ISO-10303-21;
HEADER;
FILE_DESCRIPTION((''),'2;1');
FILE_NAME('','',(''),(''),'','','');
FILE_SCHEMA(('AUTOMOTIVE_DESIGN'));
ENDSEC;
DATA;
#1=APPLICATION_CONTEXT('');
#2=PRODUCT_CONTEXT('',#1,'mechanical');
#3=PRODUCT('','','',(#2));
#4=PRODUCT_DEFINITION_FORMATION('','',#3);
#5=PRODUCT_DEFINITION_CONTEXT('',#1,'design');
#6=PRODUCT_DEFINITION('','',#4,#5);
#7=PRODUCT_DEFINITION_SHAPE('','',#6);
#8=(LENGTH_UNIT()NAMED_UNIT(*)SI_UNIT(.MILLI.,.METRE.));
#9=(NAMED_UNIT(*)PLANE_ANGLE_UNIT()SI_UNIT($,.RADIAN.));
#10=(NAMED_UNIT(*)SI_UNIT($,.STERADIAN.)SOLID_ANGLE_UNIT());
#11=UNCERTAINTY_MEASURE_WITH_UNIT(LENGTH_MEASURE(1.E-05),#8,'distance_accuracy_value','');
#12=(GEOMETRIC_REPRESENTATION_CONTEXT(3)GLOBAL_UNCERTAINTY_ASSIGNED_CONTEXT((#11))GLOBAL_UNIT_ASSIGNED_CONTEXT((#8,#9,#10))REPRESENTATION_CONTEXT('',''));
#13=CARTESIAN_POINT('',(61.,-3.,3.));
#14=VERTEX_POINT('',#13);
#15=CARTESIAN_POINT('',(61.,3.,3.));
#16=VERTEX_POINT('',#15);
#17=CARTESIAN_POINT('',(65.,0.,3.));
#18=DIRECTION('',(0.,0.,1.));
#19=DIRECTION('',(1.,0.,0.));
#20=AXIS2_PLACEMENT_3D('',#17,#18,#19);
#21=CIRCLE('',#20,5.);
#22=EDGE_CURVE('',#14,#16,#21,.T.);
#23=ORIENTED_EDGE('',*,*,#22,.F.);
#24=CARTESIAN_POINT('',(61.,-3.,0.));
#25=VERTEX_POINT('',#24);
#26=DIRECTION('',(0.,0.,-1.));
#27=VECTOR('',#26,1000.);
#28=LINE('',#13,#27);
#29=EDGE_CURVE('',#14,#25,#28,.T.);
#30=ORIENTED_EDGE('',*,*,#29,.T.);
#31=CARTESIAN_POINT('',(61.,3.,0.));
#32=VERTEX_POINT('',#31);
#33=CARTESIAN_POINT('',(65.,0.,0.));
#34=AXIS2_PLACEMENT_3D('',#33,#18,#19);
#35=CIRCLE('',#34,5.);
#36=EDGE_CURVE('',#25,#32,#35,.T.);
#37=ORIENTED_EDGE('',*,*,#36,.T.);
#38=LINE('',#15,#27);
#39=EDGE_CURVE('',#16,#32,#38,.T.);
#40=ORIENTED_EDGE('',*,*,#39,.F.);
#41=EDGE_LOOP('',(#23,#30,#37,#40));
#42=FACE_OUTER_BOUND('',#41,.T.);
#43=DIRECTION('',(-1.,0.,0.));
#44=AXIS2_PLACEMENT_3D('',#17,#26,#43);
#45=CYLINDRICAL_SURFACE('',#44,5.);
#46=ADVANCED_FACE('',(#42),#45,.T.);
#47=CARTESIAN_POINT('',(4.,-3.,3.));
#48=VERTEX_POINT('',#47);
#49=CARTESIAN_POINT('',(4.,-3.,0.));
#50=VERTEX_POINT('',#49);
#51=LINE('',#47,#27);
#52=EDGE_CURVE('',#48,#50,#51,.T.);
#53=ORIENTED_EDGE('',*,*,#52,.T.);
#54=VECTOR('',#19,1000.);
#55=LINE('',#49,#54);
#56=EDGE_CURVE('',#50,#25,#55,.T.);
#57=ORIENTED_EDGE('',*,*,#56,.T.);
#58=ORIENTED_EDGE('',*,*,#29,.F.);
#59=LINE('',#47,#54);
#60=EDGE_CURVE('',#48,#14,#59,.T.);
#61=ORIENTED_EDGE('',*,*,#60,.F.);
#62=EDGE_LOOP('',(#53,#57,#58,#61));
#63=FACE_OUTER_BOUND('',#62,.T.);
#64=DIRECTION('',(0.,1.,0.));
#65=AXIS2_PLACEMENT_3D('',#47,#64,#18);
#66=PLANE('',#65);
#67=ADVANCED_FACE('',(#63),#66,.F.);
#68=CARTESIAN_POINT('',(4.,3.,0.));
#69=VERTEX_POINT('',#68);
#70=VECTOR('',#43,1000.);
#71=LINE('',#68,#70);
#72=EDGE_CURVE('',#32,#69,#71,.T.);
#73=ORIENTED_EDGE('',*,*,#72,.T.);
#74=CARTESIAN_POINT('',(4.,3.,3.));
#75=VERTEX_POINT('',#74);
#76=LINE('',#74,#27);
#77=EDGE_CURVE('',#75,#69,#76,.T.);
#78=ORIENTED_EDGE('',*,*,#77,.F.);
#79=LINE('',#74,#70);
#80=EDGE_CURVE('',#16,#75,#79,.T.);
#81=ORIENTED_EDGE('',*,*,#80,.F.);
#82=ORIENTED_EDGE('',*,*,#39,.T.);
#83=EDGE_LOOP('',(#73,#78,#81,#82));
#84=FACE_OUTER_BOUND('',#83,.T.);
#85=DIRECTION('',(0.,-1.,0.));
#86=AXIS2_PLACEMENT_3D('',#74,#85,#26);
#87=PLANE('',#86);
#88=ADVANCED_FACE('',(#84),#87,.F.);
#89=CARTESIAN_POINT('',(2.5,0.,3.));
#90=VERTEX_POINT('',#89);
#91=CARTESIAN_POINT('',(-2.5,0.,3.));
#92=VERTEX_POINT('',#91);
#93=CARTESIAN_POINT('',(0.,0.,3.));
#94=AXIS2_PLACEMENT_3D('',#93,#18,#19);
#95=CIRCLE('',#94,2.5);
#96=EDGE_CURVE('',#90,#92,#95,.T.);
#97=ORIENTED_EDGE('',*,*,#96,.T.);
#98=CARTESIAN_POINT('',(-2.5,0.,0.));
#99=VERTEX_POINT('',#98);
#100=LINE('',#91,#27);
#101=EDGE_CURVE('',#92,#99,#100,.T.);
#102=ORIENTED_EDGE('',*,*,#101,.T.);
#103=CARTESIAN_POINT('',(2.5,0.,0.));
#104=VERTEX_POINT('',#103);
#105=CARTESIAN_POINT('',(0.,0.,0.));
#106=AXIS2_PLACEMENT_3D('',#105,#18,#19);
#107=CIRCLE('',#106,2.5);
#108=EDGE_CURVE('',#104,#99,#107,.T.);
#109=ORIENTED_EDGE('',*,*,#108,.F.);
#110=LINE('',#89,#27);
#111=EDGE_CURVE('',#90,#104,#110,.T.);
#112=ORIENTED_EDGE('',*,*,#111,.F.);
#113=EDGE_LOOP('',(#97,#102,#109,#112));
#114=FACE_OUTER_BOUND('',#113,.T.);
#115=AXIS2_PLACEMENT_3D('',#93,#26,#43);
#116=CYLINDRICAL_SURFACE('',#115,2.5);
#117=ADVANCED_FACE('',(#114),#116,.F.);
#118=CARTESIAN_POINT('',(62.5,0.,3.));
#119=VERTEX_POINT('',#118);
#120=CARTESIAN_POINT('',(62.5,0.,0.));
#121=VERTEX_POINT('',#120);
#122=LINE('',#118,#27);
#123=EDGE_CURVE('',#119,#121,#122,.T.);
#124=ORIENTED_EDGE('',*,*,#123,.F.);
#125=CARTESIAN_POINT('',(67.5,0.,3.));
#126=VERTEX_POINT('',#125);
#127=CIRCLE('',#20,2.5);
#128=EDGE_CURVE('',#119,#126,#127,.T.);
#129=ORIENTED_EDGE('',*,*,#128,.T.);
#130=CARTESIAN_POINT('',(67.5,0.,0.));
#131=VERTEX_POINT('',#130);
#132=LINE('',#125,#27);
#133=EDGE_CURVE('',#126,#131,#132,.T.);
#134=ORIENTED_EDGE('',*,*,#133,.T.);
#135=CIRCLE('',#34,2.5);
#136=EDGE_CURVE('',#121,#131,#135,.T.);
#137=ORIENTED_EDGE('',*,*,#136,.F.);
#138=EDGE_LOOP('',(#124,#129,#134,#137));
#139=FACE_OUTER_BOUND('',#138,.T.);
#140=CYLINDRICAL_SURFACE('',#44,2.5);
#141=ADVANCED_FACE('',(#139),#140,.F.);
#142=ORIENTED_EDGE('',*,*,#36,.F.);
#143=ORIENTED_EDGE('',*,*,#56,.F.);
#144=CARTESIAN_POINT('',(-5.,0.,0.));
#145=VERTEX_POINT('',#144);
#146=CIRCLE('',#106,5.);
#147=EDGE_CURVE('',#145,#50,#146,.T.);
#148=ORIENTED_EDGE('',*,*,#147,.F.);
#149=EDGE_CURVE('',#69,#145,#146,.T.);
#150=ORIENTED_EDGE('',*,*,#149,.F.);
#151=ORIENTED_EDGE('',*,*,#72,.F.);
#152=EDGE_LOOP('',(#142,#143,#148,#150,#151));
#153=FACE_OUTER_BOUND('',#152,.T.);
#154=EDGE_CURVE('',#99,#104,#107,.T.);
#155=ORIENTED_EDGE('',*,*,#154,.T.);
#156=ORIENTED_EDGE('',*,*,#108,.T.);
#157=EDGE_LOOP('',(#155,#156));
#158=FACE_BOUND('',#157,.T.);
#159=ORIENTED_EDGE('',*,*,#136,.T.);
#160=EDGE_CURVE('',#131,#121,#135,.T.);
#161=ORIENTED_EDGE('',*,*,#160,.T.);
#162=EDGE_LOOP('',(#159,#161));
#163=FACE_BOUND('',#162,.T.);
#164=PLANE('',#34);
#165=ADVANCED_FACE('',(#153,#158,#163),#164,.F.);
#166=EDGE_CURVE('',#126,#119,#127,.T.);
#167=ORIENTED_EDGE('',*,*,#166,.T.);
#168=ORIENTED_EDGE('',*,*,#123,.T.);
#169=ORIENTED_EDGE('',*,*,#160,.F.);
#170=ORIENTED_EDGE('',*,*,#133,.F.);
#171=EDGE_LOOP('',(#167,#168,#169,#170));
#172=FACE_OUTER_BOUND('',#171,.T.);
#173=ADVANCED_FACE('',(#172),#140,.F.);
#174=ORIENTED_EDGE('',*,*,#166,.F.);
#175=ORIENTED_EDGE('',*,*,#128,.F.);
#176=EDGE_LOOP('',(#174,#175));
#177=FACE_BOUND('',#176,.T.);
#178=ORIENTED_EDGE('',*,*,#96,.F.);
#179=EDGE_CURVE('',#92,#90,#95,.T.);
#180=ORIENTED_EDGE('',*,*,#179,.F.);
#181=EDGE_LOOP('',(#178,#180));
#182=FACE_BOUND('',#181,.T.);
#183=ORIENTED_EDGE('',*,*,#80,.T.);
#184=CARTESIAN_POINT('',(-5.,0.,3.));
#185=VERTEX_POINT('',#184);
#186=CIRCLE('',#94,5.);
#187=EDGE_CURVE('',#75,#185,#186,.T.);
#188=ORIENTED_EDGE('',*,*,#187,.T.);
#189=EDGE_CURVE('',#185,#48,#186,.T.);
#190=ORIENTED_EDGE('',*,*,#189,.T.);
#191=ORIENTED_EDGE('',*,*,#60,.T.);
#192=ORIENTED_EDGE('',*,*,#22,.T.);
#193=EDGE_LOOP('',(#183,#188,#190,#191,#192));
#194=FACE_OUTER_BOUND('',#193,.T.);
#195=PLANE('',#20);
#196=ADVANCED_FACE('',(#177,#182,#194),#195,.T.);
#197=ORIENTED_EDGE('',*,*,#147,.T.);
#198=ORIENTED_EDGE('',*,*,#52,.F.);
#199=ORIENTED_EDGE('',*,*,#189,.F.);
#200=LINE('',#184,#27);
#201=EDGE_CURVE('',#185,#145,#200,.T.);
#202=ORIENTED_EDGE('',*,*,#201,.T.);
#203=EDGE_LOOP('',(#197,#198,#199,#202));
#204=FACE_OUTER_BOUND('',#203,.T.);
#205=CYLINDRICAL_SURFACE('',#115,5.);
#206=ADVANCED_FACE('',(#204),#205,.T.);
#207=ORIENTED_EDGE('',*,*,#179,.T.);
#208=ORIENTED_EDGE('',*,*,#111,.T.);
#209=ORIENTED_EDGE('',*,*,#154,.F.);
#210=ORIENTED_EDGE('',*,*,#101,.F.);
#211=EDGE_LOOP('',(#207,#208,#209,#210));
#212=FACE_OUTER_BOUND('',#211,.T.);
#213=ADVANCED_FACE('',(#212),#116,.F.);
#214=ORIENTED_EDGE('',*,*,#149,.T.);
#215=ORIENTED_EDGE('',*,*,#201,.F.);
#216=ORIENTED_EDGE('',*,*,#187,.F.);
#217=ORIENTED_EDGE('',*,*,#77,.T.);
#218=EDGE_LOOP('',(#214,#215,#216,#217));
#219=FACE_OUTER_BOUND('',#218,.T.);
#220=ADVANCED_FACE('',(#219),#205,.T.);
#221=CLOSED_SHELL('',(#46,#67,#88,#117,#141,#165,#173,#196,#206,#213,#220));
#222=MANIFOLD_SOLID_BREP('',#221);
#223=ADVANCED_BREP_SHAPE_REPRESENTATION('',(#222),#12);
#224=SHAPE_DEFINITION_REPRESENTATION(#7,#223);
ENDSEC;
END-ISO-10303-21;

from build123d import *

# Parameters (mm, degrees)
SKETCH1_R           = 2.5
BOSS_EXTRUDE1_DEPTH = 3


with BuildPart() as part:
    # Sketch1 → Boss-Extrude1 (new body)
    with BuildSketch(Plane.XY):
        with BuildLine():
            Line((4, 3), (61, 3))
            ThreePointArc((61, 3), (70, 0), (61, -3))
            Line((61, -3), (4, -3))
            ThreePointArc((4, -3), (-5, 0), (4, 3))
        make_face()
        Circle(SKETCH1_R, mode=Mode.SUBTRACT)
        with Locations((65, 0)):
            Circle(SKETCH1_R, mode=Mode.SUBTRACT)
    extrude(amount=BOSS_EXTRUDE1_DEPTH)


solid = part.part
